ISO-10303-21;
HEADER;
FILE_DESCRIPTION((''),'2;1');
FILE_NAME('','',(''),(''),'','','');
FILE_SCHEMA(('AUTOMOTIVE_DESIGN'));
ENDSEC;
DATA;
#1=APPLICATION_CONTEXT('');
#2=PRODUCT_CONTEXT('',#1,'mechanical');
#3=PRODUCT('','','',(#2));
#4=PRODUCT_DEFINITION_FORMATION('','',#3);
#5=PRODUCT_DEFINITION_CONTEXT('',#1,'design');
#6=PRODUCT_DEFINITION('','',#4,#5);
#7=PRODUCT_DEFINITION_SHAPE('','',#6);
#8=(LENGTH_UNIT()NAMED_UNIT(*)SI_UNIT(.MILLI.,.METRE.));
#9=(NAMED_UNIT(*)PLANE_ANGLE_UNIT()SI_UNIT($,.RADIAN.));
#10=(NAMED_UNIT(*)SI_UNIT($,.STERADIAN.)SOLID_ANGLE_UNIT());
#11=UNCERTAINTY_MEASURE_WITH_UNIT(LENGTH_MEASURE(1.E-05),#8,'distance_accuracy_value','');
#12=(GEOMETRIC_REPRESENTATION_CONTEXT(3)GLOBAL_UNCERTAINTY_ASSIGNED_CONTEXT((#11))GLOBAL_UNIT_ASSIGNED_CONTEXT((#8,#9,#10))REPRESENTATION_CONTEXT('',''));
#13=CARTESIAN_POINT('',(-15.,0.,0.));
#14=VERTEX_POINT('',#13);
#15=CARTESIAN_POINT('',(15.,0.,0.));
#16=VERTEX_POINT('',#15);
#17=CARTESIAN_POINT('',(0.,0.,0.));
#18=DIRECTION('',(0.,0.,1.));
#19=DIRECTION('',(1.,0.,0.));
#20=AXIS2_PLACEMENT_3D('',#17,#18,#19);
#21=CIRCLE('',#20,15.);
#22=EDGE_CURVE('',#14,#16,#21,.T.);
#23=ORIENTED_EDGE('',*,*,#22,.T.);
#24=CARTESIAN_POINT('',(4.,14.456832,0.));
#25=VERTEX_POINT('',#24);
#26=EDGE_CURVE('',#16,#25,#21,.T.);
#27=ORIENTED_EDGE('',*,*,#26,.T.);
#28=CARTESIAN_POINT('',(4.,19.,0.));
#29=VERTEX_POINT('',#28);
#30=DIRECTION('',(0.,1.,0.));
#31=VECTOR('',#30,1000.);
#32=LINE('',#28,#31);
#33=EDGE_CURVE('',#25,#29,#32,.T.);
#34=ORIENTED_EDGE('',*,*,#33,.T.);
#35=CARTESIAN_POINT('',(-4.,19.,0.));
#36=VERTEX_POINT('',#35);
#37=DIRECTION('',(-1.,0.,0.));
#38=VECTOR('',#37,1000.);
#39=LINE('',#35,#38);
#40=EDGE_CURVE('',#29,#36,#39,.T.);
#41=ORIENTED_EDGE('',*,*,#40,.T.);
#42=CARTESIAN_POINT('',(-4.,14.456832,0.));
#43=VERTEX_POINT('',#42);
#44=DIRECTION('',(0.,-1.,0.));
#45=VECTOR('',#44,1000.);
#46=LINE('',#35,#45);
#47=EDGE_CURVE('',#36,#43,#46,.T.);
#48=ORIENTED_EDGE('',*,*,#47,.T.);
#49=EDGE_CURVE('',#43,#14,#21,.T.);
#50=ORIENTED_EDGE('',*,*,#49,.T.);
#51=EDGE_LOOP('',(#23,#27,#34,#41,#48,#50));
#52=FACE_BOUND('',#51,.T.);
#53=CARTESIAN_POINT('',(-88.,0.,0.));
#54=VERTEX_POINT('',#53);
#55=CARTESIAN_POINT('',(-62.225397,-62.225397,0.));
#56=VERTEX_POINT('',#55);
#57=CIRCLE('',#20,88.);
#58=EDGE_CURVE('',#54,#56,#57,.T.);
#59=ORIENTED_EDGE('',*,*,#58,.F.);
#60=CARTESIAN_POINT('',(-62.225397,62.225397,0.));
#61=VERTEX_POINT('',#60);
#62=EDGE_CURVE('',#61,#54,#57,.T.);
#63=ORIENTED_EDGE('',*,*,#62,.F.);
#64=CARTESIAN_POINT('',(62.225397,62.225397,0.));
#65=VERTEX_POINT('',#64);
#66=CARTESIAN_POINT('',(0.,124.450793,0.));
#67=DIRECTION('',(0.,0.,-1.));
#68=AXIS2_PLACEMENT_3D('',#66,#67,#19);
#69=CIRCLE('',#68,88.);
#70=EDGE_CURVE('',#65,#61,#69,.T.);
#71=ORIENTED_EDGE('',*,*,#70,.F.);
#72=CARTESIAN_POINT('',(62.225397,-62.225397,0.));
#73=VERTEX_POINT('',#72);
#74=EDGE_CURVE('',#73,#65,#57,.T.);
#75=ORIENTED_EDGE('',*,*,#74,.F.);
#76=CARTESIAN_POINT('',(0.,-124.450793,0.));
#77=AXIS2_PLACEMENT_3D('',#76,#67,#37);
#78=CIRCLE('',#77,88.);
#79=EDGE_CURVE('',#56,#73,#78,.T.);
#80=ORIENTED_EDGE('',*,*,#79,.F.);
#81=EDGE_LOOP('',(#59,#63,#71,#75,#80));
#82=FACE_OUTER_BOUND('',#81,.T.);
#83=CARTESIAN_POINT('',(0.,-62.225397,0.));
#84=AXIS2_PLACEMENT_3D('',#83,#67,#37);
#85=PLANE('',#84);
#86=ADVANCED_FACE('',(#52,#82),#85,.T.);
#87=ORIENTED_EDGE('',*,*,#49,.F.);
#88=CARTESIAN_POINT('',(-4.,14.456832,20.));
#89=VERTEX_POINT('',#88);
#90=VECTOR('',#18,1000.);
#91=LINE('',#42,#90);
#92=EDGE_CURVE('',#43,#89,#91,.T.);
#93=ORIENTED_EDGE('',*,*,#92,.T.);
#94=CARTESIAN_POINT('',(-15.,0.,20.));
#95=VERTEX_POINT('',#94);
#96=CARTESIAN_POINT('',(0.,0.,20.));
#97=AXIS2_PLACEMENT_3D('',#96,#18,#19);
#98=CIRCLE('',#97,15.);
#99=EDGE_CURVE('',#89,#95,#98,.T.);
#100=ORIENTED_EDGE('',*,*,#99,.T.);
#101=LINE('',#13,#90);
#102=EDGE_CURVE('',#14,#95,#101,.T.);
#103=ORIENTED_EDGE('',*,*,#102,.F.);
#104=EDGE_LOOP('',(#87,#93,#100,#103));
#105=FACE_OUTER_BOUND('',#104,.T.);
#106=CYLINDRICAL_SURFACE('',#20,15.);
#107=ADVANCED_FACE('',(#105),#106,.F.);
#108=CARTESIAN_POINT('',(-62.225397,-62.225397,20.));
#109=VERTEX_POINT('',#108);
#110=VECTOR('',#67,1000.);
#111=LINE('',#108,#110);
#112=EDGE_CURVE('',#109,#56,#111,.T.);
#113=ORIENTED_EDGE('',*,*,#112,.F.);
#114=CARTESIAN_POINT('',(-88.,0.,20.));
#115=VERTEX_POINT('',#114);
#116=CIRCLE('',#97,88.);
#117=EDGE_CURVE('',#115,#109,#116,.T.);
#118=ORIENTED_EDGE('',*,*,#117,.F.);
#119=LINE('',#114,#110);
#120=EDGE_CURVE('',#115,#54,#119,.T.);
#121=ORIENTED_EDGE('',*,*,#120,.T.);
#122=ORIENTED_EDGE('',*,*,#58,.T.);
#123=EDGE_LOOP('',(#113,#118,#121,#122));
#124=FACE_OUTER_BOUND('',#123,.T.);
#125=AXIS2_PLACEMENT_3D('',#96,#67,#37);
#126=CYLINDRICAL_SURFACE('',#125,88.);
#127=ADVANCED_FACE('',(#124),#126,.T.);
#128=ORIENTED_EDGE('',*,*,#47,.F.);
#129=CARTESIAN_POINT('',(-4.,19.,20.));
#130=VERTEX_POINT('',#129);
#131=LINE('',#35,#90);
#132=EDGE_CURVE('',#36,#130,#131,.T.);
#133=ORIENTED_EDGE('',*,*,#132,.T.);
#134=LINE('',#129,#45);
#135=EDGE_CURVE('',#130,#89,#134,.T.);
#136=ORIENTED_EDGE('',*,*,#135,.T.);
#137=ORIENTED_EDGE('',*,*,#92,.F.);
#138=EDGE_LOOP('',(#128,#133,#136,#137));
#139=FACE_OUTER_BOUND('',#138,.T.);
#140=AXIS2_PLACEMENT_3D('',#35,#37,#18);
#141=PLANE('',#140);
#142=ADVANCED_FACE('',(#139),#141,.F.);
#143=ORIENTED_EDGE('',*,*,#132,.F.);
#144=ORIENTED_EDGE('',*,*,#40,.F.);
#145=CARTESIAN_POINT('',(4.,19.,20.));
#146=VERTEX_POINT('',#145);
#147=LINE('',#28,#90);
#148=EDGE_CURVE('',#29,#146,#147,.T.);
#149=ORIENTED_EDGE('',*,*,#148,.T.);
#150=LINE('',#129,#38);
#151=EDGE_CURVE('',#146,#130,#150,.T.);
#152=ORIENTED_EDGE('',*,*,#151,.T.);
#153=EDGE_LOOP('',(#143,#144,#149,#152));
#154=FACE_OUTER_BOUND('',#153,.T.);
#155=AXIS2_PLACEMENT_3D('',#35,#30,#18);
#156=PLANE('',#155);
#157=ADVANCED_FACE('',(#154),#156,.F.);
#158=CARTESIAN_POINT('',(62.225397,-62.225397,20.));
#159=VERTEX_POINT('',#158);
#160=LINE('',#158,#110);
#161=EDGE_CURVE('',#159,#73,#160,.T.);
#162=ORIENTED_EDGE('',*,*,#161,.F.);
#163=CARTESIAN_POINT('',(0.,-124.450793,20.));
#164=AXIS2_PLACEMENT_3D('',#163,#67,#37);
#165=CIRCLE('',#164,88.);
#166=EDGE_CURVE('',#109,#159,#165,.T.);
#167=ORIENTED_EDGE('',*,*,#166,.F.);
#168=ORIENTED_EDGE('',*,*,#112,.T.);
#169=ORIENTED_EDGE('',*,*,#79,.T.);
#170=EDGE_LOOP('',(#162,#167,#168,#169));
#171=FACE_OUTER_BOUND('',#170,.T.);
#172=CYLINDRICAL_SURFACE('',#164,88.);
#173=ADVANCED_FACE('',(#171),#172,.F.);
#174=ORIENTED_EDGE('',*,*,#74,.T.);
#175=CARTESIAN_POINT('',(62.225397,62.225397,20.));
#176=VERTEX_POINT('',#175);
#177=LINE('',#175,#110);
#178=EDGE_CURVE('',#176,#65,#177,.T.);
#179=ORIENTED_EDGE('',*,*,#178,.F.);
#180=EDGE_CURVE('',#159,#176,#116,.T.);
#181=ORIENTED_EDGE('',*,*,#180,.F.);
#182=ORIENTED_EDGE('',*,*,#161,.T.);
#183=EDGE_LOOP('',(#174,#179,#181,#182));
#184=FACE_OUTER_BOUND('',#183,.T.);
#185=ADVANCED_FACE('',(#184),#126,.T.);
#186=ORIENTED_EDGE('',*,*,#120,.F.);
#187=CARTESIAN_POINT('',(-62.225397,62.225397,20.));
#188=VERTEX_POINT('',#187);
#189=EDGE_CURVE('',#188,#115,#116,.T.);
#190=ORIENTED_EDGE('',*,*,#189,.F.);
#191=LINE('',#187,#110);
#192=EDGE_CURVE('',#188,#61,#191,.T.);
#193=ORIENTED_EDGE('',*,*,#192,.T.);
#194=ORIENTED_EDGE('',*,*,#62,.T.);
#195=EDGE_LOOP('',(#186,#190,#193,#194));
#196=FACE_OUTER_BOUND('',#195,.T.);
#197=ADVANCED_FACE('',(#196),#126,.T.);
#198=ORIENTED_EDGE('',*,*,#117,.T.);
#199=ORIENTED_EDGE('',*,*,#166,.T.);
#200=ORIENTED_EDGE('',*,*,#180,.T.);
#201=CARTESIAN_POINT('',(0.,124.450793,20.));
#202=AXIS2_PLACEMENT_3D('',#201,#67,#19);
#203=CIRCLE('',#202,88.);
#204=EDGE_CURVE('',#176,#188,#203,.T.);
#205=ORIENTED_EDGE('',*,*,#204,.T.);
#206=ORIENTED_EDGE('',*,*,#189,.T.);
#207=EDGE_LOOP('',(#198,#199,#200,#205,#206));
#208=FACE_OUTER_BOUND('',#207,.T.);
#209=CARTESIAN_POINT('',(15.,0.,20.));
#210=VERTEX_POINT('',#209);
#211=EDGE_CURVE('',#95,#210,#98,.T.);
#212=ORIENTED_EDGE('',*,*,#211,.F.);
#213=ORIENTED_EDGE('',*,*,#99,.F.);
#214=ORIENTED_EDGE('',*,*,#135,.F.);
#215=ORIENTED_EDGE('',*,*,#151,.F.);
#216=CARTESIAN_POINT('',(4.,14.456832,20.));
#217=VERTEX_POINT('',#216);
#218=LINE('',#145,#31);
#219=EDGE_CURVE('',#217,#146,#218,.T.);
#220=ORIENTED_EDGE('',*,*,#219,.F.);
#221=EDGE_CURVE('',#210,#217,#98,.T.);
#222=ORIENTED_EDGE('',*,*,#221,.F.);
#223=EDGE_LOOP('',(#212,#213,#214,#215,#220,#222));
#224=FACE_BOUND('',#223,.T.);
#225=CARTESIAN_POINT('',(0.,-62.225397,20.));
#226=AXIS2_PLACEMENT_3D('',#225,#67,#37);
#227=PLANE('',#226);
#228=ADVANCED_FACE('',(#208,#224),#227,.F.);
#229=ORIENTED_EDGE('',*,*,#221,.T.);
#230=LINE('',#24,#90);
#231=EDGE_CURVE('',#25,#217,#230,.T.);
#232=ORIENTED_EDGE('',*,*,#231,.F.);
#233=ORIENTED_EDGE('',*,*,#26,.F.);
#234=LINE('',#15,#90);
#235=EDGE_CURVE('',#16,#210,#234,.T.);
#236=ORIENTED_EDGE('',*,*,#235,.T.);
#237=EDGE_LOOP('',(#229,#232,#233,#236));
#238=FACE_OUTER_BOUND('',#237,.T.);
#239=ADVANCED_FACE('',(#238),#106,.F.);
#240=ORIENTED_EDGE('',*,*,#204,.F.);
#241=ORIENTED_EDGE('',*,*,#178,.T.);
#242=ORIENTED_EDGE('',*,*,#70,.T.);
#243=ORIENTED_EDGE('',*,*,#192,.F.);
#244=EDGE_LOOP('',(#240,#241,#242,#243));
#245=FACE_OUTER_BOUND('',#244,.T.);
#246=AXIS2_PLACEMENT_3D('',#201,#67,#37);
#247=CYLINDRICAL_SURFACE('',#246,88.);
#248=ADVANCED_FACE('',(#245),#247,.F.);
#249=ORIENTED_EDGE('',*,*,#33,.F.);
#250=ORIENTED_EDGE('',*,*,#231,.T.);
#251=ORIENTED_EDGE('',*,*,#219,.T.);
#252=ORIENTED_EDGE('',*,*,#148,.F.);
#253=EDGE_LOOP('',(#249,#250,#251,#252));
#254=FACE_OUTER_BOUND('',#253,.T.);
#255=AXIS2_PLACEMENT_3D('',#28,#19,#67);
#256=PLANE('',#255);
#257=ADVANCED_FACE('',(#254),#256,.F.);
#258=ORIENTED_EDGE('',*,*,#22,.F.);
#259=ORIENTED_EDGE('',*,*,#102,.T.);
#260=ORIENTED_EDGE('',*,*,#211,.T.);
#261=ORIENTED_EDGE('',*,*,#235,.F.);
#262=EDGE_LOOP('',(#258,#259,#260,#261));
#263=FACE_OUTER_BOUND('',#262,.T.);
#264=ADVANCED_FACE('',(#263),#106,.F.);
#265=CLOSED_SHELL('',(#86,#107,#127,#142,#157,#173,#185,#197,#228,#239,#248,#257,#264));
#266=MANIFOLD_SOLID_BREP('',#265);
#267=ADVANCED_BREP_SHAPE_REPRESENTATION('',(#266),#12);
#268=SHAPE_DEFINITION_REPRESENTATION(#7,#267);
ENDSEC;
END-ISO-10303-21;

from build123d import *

# Parameters (mm, degrees)
EXTRUDE_1_DEPTH     = 20
CUT_EXTRUDE_1_DEPTH = 110.617516848


with BuildPart() as part:
    # 草图1 → 凸台-拉伸1 (new body)
    with BuildSketch(Plane.XY):
        with BuildLine():
            ThreePointArc((-62.225396744, 62.225396744), (-88, 0), (-62.225396744, -62.225396744))
            ThreePointArc((-62.225396744, -62.225396744), (0, -36.450793489), (62.225396744, -62.225396744))
            ThreePointArc((62.225396744, -62.225396744), (88, 0), (62.225396744, 62.225396744))
            ThreePointArc((62.225396744, 62.225396744), (0, 36.450793489), (-62.225396744, 62.225396744))
        make_face()
    extrude(amount=EXTRUDE_1_DEPTH)

    # 草图2 → 切除-拉伸1 (cut, through all)
    with BuildSketch(Plane.XY.offset(20)):
        with BuildLine():
            Line((-4, 19), (4, 19))
            Line((4, 19), (4, 14.456832295))
            ThreePointArc((4, 14.456832295), (0, -15), (-4, 14.456832295))
            Line((-4, 14.456832295), (-4, 19))
        make_face()
    extrude(amount=-CUT_EXTRUDE_1_DEPTH, mode=Mode.SUBTRACT)


solid = part.part
